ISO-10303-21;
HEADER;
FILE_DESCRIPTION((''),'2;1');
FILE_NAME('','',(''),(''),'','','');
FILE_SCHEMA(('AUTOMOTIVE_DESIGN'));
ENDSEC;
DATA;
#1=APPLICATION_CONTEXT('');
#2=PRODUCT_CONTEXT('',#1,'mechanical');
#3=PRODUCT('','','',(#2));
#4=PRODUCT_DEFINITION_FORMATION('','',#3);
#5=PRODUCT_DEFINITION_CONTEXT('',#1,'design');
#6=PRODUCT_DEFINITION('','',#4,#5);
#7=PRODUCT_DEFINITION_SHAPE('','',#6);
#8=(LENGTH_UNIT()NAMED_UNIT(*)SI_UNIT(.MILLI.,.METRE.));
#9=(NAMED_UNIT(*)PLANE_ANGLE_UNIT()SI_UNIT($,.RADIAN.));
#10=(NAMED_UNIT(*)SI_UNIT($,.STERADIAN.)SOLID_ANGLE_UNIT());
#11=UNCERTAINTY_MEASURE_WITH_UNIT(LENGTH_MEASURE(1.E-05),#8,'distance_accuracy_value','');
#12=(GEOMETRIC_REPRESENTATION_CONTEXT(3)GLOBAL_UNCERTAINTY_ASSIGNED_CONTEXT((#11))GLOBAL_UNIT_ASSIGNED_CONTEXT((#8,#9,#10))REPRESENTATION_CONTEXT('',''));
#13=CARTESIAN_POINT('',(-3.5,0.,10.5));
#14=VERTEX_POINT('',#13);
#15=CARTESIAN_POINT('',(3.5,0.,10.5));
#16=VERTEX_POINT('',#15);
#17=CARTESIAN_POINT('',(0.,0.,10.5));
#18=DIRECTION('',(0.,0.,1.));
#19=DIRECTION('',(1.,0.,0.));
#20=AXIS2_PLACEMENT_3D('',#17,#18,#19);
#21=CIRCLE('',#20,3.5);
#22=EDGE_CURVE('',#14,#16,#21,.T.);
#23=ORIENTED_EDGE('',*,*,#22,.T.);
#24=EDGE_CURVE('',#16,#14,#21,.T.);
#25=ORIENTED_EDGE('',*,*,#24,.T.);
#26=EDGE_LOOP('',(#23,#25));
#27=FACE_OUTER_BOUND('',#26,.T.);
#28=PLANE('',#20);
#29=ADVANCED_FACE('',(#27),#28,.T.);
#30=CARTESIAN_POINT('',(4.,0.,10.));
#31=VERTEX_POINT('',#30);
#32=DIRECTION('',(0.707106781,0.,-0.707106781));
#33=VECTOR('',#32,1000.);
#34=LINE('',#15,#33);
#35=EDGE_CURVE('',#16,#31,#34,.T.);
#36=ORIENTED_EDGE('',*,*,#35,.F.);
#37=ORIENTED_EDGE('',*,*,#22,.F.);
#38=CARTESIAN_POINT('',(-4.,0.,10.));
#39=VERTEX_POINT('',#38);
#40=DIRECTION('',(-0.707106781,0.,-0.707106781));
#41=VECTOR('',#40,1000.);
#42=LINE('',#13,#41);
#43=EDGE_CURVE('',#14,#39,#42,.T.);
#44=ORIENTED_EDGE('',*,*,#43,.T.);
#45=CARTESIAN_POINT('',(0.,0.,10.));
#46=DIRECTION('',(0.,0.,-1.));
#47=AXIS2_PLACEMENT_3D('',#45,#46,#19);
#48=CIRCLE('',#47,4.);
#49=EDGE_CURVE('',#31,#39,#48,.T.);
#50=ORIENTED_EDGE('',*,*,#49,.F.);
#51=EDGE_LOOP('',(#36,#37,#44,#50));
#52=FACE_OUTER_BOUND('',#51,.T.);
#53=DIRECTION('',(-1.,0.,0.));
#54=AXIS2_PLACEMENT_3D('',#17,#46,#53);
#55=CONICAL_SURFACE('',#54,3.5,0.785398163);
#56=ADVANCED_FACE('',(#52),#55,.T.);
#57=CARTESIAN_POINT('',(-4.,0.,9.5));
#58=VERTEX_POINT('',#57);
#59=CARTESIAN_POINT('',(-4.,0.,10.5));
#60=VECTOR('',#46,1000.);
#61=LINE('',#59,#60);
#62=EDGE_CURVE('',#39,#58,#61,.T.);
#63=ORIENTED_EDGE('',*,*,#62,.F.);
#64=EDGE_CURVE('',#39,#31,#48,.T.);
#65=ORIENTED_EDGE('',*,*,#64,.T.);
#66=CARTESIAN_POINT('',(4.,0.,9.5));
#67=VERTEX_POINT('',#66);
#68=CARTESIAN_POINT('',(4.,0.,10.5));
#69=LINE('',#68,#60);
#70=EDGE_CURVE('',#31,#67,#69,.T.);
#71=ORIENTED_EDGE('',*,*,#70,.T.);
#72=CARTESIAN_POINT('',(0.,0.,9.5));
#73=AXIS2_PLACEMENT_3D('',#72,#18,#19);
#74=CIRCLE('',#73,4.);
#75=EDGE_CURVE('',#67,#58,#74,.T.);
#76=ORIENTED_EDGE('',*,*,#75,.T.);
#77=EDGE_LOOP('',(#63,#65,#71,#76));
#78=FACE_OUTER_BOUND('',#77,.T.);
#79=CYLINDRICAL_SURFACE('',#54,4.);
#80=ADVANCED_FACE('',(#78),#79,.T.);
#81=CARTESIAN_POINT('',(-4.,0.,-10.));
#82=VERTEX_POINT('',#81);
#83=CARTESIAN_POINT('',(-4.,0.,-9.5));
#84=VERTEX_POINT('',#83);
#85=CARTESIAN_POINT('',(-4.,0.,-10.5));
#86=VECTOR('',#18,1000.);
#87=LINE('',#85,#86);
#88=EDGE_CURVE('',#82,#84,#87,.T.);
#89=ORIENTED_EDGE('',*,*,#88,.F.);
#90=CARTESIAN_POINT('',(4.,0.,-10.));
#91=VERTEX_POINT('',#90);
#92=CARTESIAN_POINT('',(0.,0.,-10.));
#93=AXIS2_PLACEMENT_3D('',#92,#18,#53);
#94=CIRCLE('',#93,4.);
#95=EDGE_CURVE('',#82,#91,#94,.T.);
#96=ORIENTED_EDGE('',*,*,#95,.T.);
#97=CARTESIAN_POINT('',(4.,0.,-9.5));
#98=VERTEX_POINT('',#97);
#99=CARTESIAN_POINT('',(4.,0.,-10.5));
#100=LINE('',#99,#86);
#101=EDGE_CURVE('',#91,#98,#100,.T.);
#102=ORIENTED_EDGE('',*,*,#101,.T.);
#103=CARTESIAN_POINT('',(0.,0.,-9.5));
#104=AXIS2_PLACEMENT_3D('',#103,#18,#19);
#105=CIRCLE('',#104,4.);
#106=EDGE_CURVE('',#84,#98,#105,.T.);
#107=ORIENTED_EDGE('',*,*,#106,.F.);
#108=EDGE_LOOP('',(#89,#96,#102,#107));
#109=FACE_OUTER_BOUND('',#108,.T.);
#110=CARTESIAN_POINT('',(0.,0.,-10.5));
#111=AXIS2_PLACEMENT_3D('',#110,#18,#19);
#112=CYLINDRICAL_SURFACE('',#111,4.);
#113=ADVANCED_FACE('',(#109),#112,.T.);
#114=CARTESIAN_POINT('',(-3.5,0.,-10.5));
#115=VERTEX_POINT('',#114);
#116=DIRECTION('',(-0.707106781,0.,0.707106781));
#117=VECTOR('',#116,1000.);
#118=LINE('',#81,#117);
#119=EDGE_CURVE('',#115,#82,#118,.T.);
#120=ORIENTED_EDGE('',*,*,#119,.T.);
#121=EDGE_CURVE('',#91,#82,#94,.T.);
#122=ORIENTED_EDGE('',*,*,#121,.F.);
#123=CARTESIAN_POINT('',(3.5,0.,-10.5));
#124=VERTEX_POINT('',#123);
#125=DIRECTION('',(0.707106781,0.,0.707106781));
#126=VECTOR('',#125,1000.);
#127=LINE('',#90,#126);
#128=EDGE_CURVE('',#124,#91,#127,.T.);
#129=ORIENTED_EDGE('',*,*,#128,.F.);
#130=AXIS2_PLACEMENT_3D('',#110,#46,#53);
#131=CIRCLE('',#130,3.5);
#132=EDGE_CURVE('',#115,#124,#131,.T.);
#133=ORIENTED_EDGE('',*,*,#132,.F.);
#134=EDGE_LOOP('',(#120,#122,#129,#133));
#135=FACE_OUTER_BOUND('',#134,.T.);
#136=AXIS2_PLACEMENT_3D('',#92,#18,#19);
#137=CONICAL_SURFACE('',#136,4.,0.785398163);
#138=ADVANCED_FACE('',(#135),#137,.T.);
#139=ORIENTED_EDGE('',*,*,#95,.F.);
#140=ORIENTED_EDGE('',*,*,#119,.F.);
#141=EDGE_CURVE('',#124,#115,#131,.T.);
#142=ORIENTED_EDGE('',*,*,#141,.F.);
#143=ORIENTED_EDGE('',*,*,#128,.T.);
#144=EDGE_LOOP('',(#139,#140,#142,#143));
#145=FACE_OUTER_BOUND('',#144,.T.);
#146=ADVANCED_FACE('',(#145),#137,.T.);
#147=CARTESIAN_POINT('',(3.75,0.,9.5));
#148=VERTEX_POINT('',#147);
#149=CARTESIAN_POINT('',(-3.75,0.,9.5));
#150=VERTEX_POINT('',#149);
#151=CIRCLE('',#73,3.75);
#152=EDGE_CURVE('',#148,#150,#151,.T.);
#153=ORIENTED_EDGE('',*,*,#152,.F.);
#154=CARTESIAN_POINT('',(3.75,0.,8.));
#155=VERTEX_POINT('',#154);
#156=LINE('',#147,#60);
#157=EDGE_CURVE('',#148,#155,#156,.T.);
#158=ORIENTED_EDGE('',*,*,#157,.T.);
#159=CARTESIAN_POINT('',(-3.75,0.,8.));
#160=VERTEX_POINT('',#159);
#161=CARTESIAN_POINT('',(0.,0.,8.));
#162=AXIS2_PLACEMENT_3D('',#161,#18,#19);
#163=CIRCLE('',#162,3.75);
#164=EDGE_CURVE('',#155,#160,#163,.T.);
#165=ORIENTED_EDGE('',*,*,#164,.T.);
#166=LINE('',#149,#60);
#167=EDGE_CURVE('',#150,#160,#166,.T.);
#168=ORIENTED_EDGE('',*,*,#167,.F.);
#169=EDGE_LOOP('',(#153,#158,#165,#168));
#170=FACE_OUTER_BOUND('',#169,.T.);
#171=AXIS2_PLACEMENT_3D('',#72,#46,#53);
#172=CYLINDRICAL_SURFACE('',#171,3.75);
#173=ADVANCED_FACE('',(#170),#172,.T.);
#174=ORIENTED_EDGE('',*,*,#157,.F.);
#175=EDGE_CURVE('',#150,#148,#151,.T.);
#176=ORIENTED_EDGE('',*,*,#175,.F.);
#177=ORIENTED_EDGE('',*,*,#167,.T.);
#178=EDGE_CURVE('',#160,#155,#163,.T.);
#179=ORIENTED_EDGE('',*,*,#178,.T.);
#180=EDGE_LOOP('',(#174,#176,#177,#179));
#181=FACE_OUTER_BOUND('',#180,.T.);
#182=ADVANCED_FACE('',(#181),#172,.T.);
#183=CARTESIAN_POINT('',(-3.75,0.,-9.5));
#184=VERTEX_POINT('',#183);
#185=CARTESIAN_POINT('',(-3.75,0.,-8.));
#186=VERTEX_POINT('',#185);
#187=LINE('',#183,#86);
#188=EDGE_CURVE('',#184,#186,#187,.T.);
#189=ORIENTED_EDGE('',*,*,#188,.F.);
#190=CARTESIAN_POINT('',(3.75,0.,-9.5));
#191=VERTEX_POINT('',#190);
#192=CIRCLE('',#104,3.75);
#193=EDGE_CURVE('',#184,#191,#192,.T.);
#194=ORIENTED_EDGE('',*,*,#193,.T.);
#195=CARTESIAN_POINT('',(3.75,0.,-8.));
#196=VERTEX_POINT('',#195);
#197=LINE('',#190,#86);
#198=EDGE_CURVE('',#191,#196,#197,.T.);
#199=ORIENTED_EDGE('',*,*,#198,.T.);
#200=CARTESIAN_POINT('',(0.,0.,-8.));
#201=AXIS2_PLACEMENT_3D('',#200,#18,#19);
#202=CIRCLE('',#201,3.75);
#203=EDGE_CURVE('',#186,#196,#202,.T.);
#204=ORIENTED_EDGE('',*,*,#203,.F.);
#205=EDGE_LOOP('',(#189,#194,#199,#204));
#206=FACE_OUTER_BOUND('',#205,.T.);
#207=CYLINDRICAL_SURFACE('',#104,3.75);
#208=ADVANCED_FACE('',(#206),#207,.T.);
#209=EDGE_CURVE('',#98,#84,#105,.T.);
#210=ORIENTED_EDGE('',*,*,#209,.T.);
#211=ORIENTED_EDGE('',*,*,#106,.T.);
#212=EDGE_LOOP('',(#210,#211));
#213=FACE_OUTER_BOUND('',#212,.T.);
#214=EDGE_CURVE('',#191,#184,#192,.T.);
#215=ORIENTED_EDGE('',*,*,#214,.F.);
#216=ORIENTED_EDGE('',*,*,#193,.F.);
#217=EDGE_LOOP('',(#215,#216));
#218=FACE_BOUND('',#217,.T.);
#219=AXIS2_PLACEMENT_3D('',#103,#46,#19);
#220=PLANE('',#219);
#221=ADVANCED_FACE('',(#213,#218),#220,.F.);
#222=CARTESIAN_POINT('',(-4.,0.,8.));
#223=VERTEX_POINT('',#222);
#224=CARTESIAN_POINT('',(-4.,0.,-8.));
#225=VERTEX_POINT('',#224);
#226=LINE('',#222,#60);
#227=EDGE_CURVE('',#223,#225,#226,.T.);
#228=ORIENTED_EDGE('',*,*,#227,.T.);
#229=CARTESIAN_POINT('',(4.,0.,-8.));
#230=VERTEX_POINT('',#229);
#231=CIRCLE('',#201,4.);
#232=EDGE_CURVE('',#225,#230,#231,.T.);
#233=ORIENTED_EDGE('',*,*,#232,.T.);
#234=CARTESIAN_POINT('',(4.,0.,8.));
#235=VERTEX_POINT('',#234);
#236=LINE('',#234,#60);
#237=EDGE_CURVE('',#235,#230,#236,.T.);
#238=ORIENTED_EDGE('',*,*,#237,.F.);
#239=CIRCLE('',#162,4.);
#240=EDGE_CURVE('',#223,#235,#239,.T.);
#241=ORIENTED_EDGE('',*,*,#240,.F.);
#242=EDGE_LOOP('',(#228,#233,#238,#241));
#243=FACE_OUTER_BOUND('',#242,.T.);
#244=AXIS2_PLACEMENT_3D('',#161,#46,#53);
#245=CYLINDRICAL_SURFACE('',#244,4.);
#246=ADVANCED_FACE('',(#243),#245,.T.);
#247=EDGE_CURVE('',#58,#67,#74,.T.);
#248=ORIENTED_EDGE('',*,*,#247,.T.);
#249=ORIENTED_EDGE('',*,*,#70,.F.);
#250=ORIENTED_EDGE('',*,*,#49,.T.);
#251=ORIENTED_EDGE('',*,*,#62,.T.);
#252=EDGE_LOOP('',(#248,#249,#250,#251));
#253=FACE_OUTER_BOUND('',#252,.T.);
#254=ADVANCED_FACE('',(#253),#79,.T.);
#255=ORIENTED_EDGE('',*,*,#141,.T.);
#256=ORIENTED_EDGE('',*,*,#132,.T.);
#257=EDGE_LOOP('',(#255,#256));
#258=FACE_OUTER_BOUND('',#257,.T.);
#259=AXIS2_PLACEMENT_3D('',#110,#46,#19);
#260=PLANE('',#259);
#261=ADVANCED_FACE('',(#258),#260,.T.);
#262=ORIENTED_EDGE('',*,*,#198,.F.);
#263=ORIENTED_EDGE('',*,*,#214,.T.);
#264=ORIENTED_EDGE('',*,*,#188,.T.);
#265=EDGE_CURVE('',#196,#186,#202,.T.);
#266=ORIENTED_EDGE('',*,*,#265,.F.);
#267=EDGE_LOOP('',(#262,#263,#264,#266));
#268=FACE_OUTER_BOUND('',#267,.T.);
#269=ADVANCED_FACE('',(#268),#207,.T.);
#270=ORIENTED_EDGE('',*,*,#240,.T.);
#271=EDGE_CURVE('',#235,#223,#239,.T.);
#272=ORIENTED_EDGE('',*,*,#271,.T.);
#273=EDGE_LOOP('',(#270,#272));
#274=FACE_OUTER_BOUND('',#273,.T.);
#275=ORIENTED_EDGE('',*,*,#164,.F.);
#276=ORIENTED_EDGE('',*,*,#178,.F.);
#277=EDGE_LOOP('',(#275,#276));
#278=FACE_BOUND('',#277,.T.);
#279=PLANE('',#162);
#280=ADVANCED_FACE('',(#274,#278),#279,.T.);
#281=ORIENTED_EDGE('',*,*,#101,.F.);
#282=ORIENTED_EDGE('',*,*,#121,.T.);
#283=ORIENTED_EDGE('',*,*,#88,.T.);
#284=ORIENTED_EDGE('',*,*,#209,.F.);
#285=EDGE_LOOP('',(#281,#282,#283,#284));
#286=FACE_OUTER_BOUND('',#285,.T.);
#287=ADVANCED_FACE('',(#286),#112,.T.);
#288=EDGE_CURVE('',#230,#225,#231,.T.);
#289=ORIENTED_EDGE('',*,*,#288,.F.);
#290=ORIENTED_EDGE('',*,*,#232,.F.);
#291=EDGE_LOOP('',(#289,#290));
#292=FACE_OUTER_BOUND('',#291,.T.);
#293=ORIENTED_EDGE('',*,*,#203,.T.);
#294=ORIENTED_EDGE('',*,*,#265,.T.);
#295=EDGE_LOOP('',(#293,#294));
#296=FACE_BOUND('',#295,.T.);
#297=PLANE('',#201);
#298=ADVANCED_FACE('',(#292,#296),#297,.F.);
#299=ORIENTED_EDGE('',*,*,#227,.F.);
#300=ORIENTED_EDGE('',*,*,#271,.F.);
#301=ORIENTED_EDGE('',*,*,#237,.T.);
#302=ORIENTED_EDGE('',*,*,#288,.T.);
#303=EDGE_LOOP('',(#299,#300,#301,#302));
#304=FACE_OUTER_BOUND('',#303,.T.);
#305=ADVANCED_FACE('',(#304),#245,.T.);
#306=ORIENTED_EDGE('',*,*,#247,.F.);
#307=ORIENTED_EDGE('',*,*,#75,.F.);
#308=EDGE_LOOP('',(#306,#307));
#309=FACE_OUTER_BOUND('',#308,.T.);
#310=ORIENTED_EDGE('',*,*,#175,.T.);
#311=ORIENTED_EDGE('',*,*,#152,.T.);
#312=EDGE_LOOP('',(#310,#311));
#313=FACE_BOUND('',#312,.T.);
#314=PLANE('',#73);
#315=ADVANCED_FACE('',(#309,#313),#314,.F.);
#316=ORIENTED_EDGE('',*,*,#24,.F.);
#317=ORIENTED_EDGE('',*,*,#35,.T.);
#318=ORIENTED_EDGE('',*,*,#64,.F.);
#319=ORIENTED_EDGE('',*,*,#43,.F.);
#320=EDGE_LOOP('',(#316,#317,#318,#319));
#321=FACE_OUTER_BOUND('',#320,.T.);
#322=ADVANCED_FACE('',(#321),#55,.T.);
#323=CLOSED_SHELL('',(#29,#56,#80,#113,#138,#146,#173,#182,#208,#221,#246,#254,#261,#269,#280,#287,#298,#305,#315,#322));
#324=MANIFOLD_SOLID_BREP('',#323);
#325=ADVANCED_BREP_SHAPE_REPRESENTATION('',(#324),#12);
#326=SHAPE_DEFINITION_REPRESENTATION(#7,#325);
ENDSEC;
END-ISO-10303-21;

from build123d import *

# Parameters (mm, degrees)
SKETCH1_R                = 4
BOSS_EXTRUDE1_DEPTH      = 8
SKETCH2_R                = 3.75
BOSS_EXTRUDE2_DEPTH      = 1.5
BOSS_EXTRUDE3_START      = 1
SKETCH3_R                = 4
BOSS_EXTRUDE3_DEPTH      = 1
CHAMFER1_SIZE            = 0.5
CHAMFER1_OF_MIRROR1_SIZE = 0.5


with BuildPart() as part:
    # Sketch1 → Boss-Extrude1 (new, symmetric)
    with BuildSketch(Plane.XY):
        Circle(SKETCH1_R)
    extrude(amount=BOSS_EXTRUDE1_DEPTH, both=True)

    # Sketch2 → Boss-Extrude2 (add)
    with BuildSketch(Plane.XY.offset(8)):
        Circle(SKETCH2_R)
    boss_extrude2 = extrude(amount=BOSS_EXTRUDE2_DEPTH)

    # Sketch3 → Boss-Extrude3 (add)
    with BuildSketch(Plane.XY.offset(9.5).offset(BOSS_EXTRUDE3_START)):
        Circle(SKETCH3_R)
    boss_extrude3 = extrude(amount=-BOSS_EXTRUDE3_DEPTH)

    # Chamfer1
    chamfer1_edges = [part.edges().sort_by_distance(p)[0] for p in [
        (-4, 0, 10.5),
    ]]
    chamfer(chamfer1_edges, length=CHAMFER1_SIZE)

    # Mirror1: Boss-Extrude2, Boss-Extrude3 across plane
    add(boss_extrude2.mirror(Plane.XY))
    add(boss_extrude3.mirror(Plane.XY))

    # Chamfer1 of Mirror1
    chamfer1_of_mirror1_edges = [part.edges().sort_by_distance(p)[0] for p in [
        (-4, 0, -10.5),
    ]]
    chamfer(chamfer1_of_mirror1_edges, length=CHAMFER1_OF_MIRROR1_SIZE)


solid = part.part
